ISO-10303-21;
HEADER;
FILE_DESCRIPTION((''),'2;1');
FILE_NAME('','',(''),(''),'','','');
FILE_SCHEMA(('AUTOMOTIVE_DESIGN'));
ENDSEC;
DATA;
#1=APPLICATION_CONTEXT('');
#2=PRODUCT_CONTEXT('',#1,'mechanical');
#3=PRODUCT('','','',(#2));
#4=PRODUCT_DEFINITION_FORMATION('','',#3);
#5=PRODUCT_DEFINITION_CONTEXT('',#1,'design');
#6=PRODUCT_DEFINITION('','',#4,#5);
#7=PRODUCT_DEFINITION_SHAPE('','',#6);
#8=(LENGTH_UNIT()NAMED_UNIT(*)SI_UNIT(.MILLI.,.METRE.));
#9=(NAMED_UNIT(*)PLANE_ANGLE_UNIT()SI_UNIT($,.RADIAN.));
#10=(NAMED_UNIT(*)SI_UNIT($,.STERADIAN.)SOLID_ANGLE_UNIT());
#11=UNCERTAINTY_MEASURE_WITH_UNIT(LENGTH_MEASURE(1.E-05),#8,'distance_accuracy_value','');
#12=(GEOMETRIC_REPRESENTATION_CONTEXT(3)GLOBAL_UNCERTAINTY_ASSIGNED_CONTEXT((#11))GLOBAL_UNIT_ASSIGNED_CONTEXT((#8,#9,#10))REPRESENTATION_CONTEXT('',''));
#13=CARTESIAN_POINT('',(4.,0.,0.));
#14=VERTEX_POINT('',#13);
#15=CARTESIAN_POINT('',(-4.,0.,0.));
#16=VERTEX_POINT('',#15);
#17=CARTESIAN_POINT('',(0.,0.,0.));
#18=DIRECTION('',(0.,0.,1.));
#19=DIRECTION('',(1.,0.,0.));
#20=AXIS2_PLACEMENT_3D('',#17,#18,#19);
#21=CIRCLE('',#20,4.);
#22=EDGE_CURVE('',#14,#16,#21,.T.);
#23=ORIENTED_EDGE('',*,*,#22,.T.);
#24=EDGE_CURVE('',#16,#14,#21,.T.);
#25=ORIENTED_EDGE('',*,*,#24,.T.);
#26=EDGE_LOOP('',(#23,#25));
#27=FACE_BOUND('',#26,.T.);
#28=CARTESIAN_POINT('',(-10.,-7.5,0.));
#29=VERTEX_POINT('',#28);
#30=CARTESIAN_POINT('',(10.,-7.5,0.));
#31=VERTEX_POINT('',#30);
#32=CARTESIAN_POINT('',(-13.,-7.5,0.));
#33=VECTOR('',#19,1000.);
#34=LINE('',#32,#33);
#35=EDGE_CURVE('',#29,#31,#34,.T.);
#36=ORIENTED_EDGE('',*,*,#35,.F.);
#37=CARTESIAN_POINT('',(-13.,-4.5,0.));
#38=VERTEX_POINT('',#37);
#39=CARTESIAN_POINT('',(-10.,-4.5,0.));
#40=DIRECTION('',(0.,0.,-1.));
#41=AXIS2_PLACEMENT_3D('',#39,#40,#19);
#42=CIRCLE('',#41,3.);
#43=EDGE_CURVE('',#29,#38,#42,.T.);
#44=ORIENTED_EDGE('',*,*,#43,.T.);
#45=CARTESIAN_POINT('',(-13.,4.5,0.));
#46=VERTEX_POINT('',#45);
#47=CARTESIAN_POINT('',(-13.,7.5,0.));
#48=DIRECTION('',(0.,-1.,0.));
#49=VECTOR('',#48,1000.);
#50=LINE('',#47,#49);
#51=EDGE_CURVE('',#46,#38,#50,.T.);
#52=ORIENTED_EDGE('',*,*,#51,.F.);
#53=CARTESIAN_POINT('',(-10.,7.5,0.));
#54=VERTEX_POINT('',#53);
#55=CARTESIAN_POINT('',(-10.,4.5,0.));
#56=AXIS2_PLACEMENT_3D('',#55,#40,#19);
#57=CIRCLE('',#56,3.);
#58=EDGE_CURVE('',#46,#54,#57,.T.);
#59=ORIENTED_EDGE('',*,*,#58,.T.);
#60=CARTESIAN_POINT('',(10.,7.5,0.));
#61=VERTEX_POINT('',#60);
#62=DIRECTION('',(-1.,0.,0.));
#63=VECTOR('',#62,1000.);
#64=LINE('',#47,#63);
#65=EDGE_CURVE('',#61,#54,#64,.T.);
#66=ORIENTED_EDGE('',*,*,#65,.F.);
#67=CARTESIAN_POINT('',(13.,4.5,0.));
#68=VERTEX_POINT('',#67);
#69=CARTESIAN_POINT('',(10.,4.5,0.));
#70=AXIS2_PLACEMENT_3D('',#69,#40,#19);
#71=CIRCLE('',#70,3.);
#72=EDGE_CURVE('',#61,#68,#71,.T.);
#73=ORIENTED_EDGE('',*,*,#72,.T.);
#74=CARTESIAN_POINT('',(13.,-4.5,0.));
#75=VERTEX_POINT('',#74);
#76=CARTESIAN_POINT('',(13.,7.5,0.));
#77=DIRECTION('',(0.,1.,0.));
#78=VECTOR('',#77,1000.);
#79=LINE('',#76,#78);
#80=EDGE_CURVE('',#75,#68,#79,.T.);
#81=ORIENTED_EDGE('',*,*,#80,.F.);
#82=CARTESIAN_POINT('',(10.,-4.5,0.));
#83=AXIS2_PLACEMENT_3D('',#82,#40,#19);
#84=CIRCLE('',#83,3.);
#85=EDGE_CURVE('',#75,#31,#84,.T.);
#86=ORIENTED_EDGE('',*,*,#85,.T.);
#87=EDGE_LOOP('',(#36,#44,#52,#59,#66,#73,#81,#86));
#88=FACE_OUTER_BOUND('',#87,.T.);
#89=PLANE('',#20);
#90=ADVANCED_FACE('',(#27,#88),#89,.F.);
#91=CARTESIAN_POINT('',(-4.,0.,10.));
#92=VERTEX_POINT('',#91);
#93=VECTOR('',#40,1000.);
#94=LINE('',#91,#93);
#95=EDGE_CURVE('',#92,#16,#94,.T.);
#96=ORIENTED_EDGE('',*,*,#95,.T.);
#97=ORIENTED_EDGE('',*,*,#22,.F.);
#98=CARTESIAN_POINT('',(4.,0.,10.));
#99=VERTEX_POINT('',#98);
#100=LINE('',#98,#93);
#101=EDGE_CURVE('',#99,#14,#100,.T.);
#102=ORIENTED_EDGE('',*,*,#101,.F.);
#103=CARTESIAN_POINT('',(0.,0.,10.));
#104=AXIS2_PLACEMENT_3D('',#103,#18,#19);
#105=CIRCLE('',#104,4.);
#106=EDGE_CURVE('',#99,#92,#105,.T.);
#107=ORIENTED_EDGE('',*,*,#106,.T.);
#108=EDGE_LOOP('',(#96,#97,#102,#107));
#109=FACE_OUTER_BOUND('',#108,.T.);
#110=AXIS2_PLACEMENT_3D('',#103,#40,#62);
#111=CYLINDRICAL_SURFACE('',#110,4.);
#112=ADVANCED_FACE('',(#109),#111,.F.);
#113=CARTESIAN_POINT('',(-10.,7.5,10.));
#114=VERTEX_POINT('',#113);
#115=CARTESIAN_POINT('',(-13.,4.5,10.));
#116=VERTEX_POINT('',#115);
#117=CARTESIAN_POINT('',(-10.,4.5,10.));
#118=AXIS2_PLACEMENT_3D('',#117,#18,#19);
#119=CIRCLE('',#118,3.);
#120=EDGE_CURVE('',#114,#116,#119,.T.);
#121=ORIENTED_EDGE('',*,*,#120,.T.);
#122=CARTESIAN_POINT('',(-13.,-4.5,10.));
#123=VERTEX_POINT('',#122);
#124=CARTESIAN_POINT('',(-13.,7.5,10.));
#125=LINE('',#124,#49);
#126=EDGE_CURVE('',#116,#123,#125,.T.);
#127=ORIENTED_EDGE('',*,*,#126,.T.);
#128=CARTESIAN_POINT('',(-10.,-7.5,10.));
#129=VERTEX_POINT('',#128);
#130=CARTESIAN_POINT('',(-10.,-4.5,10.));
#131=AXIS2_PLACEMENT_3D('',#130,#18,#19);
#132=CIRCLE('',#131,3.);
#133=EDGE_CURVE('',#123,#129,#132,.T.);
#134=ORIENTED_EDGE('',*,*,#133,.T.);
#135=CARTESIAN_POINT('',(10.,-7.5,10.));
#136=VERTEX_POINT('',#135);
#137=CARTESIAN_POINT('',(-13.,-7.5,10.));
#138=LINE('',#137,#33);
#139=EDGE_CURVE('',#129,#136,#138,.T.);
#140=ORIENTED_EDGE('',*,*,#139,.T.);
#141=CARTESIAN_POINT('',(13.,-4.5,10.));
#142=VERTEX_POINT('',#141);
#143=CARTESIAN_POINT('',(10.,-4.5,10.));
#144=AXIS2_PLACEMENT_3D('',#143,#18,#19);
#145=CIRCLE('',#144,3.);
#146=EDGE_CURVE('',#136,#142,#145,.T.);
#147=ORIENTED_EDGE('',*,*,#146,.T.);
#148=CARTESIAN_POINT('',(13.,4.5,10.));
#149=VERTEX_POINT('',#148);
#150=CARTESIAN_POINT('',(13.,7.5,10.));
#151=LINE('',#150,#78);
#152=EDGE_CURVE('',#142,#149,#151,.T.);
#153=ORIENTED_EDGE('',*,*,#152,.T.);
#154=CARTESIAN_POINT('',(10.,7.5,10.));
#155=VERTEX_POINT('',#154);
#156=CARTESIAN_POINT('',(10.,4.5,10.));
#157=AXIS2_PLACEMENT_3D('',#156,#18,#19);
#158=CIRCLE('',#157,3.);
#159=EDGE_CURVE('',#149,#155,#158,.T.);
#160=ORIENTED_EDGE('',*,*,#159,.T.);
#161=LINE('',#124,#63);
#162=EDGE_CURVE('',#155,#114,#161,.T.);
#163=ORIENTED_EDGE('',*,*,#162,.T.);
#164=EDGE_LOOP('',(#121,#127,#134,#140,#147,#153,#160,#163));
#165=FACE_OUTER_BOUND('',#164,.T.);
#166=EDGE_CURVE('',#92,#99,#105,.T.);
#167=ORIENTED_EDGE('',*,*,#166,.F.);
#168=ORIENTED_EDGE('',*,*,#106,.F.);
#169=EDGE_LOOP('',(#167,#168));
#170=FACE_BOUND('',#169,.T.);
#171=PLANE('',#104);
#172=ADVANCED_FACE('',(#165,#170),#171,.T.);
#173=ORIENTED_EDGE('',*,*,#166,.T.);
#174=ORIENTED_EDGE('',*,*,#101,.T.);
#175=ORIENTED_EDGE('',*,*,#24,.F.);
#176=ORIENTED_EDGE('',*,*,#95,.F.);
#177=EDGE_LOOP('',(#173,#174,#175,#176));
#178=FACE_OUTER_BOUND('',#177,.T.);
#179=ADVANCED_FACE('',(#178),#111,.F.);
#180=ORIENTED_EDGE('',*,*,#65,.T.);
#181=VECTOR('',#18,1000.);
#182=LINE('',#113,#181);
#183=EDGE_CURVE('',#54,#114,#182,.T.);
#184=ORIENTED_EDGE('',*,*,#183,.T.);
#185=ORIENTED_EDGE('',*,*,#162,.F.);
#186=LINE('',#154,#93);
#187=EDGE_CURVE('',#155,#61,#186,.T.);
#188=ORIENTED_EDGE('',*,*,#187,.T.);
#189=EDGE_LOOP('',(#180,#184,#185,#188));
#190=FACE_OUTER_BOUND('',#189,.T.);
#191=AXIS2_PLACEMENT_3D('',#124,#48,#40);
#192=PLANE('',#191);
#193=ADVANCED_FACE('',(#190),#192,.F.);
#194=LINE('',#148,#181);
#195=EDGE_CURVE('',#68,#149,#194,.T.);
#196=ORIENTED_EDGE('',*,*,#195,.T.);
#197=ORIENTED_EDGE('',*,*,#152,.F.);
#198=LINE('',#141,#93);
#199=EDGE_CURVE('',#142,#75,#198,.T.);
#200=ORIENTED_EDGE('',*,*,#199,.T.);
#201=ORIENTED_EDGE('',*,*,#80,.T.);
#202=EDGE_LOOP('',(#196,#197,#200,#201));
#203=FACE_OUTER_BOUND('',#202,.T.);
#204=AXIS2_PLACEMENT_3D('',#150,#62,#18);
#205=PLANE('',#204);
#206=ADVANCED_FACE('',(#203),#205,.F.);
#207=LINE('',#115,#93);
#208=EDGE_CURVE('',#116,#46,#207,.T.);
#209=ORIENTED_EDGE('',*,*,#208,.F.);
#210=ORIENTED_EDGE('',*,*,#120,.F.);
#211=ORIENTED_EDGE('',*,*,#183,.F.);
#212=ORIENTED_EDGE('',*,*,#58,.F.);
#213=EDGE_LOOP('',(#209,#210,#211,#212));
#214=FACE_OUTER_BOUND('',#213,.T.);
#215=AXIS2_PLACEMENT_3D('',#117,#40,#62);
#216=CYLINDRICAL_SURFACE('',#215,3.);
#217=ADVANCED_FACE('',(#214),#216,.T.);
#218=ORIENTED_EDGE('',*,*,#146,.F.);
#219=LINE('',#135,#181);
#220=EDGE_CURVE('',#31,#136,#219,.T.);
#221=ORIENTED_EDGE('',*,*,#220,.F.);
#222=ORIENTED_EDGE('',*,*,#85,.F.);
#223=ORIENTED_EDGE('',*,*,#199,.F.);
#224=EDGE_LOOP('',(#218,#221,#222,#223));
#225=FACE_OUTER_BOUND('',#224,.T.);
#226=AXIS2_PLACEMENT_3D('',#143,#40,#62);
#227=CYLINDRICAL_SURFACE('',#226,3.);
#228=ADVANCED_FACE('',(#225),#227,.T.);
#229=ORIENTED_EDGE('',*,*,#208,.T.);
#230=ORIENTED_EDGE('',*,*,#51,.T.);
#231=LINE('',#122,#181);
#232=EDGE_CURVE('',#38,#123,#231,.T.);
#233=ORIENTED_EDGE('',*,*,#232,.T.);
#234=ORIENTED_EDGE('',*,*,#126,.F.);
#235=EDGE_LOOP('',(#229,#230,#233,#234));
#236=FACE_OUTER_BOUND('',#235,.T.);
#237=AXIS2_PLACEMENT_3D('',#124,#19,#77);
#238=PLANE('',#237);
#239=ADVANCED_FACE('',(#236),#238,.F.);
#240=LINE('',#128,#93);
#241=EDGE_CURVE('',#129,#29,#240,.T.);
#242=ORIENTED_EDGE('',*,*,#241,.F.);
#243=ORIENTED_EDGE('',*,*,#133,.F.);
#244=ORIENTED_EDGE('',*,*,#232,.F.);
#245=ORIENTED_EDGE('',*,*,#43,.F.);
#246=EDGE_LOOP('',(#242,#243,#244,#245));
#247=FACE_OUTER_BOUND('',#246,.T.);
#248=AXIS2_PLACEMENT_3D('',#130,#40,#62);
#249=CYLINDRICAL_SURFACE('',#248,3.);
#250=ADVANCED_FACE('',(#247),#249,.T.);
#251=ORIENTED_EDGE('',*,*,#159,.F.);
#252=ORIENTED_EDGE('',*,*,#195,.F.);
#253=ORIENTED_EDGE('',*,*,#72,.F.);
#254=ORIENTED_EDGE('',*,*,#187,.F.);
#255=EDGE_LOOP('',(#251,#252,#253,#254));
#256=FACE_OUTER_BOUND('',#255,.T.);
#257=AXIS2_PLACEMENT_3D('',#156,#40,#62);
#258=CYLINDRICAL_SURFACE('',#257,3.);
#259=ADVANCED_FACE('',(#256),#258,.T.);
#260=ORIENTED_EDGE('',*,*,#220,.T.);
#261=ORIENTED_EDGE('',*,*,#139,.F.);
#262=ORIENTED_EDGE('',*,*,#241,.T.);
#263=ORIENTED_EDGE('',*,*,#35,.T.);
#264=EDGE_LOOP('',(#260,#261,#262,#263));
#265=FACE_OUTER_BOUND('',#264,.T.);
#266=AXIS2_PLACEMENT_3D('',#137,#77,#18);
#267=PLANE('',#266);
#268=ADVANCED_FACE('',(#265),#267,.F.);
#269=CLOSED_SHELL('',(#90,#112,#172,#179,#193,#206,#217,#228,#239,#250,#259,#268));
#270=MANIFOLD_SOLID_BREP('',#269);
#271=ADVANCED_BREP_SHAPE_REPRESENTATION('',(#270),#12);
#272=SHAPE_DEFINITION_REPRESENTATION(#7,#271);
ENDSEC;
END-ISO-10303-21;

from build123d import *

# Parameters (mm, degrees)
SKETCH1_W           = 26
SKETCH1_H           = 15
SKETCH1_R           = 4
BOSS_EXTRUDE1_DEPTH = 10
FILLET1_R           = 3


with BuildPart() as part:
    # Sketch1 → Boss-Extrude1 (new body)
    with BuildSketch(Plane.XY):
        Rectangle(SKETCH1_W, SKETCH1_H)
        Circle(SKETCH1_R, mode=Mode.SUBTRACT)
    extrude(amount=BOSS_EXTRUDE1_DEPTH)

    # Fillet1
    fillet1_edges = [part.edges().sort_by_distance(p)[0] for p in [
        (13, -7.5, 5),
        (-13, -7.5, 5),
        (-13, 7.5, 5),
        (13, 7.5, 5),
    ]]
    fillet(fillet1_edges, radius=FILLET1_R)


solid = part.part
